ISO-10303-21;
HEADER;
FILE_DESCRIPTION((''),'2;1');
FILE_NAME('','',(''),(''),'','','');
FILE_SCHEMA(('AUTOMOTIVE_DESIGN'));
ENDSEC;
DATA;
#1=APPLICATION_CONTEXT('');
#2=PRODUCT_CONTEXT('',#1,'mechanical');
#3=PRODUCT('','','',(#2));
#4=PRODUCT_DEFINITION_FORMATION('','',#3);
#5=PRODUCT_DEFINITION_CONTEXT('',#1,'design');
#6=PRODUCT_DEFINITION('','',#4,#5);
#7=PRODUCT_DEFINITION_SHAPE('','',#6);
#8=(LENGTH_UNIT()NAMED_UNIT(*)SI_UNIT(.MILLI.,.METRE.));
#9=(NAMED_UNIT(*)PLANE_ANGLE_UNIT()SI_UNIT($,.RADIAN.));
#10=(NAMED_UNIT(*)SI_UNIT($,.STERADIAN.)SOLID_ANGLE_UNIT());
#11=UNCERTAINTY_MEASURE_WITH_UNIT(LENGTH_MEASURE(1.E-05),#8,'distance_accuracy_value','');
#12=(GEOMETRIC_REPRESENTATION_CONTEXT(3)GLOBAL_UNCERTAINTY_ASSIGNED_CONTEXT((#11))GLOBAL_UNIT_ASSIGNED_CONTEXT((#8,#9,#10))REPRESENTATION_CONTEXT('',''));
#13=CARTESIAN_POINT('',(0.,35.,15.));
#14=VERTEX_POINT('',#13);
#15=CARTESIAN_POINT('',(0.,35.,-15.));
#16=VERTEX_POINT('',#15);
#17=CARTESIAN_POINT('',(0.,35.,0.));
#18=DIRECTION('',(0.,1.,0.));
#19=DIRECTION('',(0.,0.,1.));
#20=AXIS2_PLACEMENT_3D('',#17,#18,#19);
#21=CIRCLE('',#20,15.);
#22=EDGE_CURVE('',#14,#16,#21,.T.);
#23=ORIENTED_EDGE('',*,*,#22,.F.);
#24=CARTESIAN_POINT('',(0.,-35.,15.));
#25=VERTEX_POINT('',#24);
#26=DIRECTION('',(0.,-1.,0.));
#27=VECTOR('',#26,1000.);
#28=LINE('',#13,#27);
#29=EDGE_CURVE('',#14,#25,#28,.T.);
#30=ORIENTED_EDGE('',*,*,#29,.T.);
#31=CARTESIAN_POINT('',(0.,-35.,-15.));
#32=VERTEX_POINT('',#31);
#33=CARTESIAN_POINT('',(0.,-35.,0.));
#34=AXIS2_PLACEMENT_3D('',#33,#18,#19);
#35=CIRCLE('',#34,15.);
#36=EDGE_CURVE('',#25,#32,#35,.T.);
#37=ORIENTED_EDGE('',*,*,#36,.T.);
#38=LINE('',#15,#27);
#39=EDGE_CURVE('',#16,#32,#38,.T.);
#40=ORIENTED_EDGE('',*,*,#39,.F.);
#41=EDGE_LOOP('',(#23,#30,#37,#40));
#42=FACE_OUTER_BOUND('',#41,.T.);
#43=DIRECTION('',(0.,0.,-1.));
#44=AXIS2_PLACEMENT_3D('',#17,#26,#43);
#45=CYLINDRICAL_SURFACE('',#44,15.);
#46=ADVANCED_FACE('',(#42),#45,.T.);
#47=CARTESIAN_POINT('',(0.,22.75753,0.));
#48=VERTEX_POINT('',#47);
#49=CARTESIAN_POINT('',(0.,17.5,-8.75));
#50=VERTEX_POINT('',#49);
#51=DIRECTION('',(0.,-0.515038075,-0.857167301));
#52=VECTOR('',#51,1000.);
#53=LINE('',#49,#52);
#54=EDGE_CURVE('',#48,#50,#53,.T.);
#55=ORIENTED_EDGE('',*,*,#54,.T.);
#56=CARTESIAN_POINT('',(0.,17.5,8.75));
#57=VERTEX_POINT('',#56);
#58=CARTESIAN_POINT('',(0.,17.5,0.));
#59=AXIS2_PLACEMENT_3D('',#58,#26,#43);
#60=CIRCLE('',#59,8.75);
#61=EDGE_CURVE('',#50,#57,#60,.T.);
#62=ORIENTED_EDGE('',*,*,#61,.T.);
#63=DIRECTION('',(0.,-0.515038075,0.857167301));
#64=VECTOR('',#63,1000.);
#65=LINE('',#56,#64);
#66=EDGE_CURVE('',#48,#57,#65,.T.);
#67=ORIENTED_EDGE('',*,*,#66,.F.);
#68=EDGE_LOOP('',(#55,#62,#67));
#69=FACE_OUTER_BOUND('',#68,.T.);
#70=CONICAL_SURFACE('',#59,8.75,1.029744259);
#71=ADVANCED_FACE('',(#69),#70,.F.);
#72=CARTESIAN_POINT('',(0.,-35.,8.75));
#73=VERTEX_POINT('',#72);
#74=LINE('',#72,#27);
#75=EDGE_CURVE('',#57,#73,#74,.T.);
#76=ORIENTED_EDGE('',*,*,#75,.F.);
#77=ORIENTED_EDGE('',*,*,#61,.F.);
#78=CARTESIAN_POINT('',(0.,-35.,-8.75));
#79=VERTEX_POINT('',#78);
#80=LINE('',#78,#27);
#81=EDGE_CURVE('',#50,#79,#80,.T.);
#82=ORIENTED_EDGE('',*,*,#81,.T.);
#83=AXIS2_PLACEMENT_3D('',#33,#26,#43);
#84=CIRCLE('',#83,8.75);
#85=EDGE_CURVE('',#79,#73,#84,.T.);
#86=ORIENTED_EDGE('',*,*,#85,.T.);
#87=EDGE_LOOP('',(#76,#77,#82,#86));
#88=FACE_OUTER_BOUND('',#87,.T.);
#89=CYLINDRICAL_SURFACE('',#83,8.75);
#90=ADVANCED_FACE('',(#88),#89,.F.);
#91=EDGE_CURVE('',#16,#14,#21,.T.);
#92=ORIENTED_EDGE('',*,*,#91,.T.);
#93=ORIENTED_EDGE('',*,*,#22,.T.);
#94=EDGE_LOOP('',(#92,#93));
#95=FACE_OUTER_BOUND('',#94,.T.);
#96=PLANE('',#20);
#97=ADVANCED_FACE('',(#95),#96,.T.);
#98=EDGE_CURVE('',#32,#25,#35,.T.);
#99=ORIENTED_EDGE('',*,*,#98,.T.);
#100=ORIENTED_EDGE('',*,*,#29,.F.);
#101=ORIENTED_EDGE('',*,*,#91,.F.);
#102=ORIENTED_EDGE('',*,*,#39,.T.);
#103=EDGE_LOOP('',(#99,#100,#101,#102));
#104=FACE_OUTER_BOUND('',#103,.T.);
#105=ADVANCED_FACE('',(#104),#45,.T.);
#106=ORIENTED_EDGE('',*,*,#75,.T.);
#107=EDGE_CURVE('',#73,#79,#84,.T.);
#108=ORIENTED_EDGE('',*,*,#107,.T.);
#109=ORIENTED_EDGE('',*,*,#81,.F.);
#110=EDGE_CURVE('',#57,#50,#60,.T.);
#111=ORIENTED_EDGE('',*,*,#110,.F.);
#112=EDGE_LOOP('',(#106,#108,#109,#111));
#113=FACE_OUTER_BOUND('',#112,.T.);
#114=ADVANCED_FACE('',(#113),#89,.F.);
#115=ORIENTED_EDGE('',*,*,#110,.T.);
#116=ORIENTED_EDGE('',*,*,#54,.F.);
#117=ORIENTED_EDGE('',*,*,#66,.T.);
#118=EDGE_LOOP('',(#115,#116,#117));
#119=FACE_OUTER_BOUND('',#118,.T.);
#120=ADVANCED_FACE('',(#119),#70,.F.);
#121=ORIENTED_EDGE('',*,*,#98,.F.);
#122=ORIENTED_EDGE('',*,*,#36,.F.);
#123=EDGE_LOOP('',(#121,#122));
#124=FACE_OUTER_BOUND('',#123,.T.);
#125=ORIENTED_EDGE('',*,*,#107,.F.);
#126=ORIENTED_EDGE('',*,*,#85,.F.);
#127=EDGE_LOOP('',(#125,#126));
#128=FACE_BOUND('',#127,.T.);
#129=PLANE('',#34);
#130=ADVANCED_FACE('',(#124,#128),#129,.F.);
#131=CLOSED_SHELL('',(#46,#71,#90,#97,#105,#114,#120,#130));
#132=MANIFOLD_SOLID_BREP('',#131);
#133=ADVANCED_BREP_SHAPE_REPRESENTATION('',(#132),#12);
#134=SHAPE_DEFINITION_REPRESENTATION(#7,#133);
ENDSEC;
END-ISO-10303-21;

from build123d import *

# Parameters (mm, degrees)
SKETCH1_R              = 15
BOSS_EXTRUDE1_DEPTH    = 35
M20_TAPPED_HOLE1_D     = 17.5
M20_TAPPED_HOLE1_DEPTH = 52.5
M20_TAPPED_HOLE1_TIP   = 5.257530416


with BuildPart() as part:
    # Sketch1 → Boss-Extrude1 (new, symmetric)
    with BuildSketch(Plane(origin=(0, 0, 0), x_dir=(1, 0, 0), z_dir=(0, 1, 0))):
        with Locations(Location((0, 0, 0), (0, 0, 270))):
            Circle(SKETCH1_R)
    extrude(amount=BOSS_EXTRUDE1_DEPTH, both=True)

    # M20 Tapped Hole1
    with Locations(Plane(origin=(0, -35, 0), x_dir=(0, 0, -1), z_dir=(0, -1, 0))):
        with Locations((0, 0)):
            Hole(M20_TAPPED_HOLE1_D / 2, depth=M20_TAPPED_HOLE1_DEPTH)
            with Locations((0, 0, -(M20_TAPPED_HOLE1_DEPTH + M20_TAPPED_HOLE1_TIP / 2))):  # 118° drill point
                Cone(0, M20_TAPPED_HOLE1_D / 2, M20_TAPPED_HOLE1_TIP, mode=Mode.SUBTRACT)


solid = part.part
